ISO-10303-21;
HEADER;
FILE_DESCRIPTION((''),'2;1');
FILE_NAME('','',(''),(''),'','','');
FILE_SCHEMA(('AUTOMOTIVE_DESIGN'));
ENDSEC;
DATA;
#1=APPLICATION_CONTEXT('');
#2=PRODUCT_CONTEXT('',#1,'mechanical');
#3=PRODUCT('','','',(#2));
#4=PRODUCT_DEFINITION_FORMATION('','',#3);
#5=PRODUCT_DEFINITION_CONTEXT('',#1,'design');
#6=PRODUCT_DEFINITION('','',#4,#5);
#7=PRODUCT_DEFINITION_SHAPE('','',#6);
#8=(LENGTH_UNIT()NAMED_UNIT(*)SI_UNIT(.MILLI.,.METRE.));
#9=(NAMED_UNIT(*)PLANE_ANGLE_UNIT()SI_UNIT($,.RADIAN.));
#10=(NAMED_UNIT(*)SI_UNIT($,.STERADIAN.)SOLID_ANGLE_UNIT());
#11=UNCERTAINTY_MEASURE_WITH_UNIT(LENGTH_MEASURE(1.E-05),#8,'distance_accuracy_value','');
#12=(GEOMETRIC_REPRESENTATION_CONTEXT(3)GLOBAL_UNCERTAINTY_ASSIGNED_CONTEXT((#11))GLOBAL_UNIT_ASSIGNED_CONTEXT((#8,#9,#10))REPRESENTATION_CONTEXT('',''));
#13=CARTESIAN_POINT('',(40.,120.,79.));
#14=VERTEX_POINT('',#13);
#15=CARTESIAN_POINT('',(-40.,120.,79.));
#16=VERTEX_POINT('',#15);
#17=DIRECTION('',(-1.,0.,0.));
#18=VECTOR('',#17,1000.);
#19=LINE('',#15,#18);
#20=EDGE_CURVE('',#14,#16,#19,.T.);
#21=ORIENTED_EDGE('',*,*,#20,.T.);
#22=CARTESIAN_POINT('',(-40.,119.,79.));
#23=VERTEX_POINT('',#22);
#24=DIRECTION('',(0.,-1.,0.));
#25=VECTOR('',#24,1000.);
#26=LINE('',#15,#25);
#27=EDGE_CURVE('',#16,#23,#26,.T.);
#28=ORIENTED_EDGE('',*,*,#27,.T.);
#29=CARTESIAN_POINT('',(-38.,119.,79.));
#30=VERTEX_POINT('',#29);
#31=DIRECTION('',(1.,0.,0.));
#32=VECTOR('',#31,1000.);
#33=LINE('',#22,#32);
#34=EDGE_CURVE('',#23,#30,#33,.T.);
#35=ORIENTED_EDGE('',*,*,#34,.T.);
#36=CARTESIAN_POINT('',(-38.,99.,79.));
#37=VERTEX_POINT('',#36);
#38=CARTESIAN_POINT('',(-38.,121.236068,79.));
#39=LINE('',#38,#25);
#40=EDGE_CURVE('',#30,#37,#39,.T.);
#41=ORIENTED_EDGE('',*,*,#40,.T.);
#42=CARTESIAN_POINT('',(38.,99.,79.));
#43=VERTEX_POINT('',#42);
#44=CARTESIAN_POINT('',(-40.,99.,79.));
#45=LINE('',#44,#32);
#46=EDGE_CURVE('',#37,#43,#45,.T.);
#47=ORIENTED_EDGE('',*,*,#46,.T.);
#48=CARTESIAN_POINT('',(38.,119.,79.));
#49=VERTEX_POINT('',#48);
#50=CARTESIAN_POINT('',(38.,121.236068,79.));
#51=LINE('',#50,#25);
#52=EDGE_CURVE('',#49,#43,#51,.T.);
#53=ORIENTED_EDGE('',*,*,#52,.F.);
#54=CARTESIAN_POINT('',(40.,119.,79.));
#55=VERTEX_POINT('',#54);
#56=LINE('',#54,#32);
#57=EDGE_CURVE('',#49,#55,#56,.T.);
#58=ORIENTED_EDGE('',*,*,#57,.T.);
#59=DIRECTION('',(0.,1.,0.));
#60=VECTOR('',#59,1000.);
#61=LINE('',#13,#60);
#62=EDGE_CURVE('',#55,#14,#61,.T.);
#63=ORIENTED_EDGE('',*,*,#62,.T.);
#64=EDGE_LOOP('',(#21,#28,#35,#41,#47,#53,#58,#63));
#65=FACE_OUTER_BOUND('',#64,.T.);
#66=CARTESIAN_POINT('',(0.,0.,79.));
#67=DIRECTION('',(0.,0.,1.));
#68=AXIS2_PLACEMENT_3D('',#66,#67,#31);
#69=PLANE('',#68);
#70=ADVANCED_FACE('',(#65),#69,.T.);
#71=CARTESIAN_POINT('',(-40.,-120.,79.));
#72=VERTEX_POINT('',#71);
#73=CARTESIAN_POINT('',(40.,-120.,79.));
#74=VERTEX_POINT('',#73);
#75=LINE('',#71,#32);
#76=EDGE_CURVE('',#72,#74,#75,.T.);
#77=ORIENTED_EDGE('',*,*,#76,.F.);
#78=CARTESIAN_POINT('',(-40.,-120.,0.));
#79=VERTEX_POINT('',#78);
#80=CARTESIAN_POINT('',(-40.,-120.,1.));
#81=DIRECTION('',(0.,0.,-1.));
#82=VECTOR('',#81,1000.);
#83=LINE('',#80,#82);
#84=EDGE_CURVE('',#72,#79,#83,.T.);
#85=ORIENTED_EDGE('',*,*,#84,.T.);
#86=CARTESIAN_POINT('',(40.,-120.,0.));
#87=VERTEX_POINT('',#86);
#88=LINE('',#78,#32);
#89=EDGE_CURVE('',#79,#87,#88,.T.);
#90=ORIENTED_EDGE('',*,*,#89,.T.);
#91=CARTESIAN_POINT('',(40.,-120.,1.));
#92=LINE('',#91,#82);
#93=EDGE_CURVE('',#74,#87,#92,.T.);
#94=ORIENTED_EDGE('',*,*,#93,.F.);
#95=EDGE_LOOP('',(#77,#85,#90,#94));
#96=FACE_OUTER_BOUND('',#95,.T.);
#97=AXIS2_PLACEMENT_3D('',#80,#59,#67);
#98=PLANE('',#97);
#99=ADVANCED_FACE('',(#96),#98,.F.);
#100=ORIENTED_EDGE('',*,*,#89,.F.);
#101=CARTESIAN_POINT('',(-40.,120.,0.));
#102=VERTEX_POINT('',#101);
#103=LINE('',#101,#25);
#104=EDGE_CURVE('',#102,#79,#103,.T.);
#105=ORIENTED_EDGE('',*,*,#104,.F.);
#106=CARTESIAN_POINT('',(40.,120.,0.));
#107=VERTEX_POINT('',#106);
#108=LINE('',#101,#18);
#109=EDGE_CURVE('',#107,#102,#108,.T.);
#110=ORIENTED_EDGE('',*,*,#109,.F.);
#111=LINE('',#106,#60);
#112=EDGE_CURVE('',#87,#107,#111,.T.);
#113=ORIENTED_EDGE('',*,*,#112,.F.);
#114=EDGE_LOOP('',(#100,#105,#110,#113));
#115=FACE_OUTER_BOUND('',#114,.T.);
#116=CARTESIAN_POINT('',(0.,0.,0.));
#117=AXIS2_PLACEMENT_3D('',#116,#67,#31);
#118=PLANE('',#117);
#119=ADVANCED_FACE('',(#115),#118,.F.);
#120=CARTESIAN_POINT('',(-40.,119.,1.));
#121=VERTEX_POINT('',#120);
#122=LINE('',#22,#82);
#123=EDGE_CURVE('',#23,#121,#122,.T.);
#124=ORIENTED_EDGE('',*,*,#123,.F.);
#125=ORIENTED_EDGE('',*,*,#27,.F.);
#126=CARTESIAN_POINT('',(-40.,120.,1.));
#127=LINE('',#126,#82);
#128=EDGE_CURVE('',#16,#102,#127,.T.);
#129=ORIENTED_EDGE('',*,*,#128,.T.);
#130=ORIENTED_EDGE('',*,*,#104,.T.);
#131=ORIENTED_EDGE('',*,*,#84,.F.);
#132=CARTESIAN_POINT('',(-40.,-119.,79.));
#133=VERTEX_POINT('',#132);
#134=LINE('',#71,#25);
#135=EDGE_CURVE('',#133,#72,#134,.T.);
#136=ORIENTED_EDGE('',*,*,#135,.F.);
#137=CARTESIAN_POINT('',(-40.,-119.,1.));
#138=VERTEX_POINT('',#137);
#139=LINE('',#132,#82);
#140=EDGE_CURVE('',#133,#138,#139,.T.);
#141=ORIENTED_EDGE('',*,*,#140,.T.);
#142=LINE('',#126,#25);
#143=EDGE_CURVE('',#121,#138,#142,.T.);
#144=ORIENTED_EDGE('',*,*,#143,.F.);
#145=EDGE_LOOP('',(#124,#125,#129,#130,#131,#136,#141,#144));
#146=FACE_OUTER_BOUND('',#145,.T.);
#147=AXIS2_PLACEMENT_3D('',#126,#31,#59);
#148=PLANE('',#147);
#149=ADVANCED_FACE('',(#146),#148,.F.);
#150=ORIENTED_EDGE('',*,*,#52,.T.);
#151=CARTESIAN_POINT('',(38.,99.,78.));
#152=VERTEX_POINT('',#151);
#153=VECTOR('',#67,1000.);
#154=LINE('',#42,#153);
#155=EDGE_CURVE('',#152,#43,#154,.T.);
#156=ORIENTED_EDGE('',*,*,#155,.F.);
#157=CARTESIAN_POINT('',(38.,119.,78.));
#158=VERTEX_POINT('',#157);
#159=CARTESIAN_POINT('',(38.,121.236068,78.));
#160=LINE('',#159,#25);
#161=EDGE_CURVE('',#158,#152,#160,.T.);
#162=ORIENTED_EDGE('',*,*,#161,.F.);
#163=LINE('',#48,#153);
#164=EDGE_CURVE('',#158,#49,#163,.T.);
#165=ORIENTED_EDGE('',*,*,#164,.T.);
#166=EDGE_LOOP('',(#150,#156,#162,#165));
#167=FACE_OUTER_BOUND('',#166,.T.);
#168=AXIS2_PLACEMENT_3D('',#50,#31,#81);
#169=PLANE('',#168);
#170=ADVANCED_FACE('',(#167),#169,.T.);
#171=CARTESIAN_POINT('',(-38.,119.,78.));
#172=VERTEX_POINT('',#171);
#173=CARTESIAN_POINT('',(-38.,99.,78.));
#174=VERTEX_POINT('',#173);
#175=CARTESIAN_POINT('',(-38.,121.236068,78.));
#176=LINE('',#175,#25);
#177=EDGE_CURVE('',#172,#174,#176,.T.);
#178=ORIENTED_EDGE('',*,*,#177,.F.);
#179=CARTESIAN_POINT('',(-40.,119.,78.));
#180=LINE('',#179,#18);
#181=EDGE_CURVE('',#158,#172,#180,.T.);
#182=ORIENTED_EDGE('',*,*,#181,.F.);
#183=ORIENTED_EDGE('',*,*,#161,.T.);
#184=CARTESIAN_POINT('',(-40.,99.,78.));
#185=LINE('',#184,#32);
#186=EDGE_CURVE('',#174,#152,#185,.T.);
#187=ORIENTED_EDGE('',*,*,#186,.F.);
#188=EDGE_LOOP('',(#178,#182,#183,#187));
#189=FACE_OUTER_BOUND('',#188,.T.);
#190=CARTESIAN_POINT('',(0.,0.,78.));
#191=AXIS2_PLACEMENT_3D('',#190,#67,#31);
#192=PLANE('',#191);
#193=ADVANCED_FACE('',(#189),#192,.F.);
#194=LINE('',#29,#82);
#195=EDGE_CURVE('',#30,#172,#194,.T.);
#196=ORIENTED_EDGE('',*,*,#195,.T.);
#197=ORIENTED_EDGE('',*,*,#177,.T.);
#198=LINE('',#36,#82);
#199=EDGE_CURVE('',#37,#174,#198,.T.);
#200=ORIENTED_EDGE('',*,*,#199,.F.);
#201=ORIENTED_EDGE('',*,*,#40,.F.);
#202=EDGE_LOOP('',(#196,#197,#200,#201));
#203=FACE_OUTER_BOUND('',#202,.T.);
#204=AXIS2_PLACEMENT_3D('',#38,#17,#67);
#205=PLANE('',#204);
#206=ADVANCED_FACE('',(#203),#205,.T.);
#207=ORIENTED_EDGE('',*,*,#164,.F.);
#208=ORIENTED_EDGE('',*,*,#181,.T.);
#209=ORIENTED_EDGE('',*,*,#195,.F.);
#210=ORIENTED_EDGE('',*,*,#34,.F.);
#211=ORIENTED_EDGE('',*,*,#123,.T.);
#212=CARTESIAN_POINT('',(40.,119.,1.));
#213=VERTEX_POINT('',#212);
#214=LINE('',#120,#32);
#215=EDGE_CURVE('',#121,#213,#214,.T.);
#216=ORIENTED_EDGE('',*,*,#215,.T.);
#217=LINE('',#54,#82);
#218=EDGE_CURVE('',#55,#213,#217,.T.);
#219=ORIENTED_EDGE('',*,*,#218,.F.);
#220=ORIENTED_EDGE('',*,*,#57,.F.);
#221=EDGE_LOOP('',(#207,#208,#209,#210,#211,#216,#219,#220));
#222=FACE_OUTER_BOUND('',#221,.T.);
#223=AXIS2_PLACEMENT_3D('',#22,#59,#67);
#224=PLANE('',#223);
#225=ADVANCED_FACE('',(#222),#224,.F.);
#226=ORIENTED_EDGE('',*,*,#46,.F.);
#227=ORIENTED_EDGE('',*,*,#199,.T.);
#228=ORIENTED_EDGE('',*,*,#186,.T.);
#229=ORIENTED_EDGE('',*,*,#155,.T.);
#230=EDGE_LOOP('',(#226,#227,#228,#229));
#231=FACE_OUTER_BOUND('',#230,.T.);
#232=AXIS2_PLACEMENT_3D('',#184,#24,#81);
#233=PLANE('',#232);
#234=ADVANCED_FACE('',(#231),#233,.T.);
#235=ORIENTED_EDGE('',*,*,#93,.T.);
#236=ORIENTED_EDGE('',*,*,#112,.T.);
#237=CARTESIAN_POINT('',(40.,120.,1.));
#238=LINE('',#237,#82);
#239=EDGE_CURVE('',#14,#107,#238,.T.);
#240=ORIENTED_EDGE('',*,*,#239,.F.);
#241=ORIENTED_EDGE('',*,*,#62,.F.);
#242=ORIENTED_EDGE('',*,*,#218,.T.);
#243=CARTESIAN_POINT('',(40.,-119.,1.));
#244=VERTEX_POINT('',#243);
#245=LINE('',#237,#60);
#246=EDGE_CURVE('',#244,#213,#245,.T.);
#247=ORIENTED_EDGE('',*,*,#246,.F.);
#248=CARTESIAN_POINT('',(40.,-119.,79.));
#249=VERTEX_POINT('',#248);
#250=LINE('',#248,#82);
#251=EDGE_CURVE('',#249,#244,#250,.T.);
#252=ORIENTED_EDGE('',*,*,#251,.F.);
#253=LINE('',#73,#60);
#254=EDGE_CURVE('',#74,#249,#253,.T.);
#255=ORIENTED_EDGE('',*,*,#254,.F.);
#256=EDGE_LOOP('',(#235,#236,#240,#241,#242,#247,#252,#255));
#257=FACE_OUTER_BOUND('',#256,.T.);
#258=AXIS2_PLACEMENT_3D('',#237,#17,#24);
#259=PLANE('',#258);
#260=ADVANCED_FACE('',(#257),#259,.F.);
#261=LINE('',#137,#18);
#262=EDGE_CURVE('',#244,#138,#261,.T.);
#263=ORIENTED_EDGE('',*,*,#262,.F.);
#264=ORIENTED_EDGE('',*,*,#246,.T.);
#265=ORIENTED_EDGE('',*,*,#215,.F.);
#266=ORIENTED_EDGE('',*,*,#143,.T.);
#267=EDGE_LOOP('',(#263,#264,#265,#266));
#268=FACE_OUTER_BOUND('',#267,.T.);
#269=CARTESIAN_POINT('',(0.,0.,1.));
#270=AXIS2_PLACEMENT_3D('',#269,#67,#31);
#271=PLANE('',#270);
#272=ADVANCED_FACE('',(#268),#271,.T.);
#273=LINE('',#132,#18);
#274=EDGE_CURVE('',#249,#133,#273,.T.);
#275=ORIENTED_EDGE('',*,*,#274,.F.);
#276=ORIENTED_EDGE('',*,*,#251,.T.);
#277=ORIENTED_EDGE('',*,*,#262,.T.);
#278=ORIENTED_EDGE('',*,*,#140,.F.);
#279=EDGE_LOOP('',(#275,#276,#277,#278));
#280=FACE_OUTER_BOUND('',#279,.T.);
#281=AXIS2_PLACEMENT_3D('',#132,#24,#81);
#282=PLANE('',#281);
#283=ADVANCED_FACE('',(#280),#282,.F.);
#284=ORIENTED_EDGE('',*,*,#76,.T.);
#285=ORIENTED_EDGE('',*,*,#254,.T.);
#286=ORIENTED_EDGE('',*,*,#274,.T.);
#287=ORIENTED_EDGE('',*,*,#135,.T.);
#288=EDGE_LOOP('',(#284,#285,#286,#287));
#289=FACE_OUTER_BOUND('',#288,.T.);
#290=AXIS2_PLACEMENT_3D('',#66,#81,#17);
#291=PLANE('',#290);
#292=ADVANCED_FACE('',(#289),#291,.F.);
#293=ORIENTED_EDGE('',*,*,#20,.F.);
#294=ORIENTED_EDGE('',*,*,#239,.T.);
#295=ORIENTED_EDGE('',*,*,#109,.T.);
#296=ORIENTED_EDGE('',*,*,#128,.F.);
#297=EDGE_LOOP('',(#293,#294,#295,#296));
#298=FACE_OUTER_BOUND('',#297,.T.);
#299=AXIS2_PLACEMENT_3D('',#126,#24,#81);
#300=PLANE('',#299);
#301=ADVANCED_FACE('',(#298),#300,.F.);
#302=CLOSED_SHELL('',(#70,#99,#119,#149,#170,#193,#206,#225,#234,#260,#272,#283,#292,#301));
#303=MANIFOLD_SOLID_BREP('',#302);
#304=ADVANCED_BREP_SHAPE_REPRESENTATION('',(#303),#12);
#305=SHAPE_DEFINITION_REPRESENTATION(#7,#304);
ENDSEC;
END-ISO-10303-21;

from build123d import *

# Parameters (mm, degrees)
SKETCH1_W           = 80
SKETCH1_H           = 240
BOSS_EXTRUDE1_DEPTH = 1
SKETCH2_W           = 80
SKETCH2_H           = 1
BOSS_EXTRUDE2_DEPTH = 78
SKETCH3_W           = 80
SKETCH3_H           = 20
BOSS_EXTRUDE3_DEPTH = 1
SKETCH4_W           = 2
SKETCH4_H           = 1
CUT_EXTRUDE1_DEPTH  = 20


with BuildPart() as part:
    # Sketch1 → Boss-Extrude1 (new body)
    with BuildSketch(Plane.XY):
        Rectangle(SKETCH1_W, SKETCH1_H)
    extrude(amount=BOSS_EXTRUDE1_DEPTH)

    # Sketch2 → Boss-Extrude2 (add)
    with BuildSketch(Plane.XY.offset(1)):
        with Locations((0, 119.5)):
            Rectangle(SKETCH2_W, SKETCH2_H)
        with Locations((0, -119.5)):
            Rectangle(SKETCH2_W, SKETCH2_H)
    extrude(amount=BOSS_EXTRUDE2_DEPTH)

    # Sketch3 → Boss-Extrude3 (add)
    with BuildSketch(Plane.XY.offset(79)):
        with Locations((0, 109)):
            Rectangle(SKETCH3_W, SKETCH3_H)
    extrude(amount=-BOSS_EXTRUDE3_DEPTH)

    # Sketch4 → Cut-Extrude1 (cut)
    with BuildSketch(Plane(origin=(0, 99, 0), x_dir=(1, 0, 0), z_dir=(0, 1, 0))):
        with Locations((-39, -78.5)):
            Rectangle(SKETCH4_W, SKETCH4_H)
        with Locations((39, -78.5)):
            Rectangle(SKETCH4_W, SKETCH4_H)
    extrude(amount=CUT_EXTRUDE1_DEPTH, mode=Mode.SUBTRACT)


solid = part.part
